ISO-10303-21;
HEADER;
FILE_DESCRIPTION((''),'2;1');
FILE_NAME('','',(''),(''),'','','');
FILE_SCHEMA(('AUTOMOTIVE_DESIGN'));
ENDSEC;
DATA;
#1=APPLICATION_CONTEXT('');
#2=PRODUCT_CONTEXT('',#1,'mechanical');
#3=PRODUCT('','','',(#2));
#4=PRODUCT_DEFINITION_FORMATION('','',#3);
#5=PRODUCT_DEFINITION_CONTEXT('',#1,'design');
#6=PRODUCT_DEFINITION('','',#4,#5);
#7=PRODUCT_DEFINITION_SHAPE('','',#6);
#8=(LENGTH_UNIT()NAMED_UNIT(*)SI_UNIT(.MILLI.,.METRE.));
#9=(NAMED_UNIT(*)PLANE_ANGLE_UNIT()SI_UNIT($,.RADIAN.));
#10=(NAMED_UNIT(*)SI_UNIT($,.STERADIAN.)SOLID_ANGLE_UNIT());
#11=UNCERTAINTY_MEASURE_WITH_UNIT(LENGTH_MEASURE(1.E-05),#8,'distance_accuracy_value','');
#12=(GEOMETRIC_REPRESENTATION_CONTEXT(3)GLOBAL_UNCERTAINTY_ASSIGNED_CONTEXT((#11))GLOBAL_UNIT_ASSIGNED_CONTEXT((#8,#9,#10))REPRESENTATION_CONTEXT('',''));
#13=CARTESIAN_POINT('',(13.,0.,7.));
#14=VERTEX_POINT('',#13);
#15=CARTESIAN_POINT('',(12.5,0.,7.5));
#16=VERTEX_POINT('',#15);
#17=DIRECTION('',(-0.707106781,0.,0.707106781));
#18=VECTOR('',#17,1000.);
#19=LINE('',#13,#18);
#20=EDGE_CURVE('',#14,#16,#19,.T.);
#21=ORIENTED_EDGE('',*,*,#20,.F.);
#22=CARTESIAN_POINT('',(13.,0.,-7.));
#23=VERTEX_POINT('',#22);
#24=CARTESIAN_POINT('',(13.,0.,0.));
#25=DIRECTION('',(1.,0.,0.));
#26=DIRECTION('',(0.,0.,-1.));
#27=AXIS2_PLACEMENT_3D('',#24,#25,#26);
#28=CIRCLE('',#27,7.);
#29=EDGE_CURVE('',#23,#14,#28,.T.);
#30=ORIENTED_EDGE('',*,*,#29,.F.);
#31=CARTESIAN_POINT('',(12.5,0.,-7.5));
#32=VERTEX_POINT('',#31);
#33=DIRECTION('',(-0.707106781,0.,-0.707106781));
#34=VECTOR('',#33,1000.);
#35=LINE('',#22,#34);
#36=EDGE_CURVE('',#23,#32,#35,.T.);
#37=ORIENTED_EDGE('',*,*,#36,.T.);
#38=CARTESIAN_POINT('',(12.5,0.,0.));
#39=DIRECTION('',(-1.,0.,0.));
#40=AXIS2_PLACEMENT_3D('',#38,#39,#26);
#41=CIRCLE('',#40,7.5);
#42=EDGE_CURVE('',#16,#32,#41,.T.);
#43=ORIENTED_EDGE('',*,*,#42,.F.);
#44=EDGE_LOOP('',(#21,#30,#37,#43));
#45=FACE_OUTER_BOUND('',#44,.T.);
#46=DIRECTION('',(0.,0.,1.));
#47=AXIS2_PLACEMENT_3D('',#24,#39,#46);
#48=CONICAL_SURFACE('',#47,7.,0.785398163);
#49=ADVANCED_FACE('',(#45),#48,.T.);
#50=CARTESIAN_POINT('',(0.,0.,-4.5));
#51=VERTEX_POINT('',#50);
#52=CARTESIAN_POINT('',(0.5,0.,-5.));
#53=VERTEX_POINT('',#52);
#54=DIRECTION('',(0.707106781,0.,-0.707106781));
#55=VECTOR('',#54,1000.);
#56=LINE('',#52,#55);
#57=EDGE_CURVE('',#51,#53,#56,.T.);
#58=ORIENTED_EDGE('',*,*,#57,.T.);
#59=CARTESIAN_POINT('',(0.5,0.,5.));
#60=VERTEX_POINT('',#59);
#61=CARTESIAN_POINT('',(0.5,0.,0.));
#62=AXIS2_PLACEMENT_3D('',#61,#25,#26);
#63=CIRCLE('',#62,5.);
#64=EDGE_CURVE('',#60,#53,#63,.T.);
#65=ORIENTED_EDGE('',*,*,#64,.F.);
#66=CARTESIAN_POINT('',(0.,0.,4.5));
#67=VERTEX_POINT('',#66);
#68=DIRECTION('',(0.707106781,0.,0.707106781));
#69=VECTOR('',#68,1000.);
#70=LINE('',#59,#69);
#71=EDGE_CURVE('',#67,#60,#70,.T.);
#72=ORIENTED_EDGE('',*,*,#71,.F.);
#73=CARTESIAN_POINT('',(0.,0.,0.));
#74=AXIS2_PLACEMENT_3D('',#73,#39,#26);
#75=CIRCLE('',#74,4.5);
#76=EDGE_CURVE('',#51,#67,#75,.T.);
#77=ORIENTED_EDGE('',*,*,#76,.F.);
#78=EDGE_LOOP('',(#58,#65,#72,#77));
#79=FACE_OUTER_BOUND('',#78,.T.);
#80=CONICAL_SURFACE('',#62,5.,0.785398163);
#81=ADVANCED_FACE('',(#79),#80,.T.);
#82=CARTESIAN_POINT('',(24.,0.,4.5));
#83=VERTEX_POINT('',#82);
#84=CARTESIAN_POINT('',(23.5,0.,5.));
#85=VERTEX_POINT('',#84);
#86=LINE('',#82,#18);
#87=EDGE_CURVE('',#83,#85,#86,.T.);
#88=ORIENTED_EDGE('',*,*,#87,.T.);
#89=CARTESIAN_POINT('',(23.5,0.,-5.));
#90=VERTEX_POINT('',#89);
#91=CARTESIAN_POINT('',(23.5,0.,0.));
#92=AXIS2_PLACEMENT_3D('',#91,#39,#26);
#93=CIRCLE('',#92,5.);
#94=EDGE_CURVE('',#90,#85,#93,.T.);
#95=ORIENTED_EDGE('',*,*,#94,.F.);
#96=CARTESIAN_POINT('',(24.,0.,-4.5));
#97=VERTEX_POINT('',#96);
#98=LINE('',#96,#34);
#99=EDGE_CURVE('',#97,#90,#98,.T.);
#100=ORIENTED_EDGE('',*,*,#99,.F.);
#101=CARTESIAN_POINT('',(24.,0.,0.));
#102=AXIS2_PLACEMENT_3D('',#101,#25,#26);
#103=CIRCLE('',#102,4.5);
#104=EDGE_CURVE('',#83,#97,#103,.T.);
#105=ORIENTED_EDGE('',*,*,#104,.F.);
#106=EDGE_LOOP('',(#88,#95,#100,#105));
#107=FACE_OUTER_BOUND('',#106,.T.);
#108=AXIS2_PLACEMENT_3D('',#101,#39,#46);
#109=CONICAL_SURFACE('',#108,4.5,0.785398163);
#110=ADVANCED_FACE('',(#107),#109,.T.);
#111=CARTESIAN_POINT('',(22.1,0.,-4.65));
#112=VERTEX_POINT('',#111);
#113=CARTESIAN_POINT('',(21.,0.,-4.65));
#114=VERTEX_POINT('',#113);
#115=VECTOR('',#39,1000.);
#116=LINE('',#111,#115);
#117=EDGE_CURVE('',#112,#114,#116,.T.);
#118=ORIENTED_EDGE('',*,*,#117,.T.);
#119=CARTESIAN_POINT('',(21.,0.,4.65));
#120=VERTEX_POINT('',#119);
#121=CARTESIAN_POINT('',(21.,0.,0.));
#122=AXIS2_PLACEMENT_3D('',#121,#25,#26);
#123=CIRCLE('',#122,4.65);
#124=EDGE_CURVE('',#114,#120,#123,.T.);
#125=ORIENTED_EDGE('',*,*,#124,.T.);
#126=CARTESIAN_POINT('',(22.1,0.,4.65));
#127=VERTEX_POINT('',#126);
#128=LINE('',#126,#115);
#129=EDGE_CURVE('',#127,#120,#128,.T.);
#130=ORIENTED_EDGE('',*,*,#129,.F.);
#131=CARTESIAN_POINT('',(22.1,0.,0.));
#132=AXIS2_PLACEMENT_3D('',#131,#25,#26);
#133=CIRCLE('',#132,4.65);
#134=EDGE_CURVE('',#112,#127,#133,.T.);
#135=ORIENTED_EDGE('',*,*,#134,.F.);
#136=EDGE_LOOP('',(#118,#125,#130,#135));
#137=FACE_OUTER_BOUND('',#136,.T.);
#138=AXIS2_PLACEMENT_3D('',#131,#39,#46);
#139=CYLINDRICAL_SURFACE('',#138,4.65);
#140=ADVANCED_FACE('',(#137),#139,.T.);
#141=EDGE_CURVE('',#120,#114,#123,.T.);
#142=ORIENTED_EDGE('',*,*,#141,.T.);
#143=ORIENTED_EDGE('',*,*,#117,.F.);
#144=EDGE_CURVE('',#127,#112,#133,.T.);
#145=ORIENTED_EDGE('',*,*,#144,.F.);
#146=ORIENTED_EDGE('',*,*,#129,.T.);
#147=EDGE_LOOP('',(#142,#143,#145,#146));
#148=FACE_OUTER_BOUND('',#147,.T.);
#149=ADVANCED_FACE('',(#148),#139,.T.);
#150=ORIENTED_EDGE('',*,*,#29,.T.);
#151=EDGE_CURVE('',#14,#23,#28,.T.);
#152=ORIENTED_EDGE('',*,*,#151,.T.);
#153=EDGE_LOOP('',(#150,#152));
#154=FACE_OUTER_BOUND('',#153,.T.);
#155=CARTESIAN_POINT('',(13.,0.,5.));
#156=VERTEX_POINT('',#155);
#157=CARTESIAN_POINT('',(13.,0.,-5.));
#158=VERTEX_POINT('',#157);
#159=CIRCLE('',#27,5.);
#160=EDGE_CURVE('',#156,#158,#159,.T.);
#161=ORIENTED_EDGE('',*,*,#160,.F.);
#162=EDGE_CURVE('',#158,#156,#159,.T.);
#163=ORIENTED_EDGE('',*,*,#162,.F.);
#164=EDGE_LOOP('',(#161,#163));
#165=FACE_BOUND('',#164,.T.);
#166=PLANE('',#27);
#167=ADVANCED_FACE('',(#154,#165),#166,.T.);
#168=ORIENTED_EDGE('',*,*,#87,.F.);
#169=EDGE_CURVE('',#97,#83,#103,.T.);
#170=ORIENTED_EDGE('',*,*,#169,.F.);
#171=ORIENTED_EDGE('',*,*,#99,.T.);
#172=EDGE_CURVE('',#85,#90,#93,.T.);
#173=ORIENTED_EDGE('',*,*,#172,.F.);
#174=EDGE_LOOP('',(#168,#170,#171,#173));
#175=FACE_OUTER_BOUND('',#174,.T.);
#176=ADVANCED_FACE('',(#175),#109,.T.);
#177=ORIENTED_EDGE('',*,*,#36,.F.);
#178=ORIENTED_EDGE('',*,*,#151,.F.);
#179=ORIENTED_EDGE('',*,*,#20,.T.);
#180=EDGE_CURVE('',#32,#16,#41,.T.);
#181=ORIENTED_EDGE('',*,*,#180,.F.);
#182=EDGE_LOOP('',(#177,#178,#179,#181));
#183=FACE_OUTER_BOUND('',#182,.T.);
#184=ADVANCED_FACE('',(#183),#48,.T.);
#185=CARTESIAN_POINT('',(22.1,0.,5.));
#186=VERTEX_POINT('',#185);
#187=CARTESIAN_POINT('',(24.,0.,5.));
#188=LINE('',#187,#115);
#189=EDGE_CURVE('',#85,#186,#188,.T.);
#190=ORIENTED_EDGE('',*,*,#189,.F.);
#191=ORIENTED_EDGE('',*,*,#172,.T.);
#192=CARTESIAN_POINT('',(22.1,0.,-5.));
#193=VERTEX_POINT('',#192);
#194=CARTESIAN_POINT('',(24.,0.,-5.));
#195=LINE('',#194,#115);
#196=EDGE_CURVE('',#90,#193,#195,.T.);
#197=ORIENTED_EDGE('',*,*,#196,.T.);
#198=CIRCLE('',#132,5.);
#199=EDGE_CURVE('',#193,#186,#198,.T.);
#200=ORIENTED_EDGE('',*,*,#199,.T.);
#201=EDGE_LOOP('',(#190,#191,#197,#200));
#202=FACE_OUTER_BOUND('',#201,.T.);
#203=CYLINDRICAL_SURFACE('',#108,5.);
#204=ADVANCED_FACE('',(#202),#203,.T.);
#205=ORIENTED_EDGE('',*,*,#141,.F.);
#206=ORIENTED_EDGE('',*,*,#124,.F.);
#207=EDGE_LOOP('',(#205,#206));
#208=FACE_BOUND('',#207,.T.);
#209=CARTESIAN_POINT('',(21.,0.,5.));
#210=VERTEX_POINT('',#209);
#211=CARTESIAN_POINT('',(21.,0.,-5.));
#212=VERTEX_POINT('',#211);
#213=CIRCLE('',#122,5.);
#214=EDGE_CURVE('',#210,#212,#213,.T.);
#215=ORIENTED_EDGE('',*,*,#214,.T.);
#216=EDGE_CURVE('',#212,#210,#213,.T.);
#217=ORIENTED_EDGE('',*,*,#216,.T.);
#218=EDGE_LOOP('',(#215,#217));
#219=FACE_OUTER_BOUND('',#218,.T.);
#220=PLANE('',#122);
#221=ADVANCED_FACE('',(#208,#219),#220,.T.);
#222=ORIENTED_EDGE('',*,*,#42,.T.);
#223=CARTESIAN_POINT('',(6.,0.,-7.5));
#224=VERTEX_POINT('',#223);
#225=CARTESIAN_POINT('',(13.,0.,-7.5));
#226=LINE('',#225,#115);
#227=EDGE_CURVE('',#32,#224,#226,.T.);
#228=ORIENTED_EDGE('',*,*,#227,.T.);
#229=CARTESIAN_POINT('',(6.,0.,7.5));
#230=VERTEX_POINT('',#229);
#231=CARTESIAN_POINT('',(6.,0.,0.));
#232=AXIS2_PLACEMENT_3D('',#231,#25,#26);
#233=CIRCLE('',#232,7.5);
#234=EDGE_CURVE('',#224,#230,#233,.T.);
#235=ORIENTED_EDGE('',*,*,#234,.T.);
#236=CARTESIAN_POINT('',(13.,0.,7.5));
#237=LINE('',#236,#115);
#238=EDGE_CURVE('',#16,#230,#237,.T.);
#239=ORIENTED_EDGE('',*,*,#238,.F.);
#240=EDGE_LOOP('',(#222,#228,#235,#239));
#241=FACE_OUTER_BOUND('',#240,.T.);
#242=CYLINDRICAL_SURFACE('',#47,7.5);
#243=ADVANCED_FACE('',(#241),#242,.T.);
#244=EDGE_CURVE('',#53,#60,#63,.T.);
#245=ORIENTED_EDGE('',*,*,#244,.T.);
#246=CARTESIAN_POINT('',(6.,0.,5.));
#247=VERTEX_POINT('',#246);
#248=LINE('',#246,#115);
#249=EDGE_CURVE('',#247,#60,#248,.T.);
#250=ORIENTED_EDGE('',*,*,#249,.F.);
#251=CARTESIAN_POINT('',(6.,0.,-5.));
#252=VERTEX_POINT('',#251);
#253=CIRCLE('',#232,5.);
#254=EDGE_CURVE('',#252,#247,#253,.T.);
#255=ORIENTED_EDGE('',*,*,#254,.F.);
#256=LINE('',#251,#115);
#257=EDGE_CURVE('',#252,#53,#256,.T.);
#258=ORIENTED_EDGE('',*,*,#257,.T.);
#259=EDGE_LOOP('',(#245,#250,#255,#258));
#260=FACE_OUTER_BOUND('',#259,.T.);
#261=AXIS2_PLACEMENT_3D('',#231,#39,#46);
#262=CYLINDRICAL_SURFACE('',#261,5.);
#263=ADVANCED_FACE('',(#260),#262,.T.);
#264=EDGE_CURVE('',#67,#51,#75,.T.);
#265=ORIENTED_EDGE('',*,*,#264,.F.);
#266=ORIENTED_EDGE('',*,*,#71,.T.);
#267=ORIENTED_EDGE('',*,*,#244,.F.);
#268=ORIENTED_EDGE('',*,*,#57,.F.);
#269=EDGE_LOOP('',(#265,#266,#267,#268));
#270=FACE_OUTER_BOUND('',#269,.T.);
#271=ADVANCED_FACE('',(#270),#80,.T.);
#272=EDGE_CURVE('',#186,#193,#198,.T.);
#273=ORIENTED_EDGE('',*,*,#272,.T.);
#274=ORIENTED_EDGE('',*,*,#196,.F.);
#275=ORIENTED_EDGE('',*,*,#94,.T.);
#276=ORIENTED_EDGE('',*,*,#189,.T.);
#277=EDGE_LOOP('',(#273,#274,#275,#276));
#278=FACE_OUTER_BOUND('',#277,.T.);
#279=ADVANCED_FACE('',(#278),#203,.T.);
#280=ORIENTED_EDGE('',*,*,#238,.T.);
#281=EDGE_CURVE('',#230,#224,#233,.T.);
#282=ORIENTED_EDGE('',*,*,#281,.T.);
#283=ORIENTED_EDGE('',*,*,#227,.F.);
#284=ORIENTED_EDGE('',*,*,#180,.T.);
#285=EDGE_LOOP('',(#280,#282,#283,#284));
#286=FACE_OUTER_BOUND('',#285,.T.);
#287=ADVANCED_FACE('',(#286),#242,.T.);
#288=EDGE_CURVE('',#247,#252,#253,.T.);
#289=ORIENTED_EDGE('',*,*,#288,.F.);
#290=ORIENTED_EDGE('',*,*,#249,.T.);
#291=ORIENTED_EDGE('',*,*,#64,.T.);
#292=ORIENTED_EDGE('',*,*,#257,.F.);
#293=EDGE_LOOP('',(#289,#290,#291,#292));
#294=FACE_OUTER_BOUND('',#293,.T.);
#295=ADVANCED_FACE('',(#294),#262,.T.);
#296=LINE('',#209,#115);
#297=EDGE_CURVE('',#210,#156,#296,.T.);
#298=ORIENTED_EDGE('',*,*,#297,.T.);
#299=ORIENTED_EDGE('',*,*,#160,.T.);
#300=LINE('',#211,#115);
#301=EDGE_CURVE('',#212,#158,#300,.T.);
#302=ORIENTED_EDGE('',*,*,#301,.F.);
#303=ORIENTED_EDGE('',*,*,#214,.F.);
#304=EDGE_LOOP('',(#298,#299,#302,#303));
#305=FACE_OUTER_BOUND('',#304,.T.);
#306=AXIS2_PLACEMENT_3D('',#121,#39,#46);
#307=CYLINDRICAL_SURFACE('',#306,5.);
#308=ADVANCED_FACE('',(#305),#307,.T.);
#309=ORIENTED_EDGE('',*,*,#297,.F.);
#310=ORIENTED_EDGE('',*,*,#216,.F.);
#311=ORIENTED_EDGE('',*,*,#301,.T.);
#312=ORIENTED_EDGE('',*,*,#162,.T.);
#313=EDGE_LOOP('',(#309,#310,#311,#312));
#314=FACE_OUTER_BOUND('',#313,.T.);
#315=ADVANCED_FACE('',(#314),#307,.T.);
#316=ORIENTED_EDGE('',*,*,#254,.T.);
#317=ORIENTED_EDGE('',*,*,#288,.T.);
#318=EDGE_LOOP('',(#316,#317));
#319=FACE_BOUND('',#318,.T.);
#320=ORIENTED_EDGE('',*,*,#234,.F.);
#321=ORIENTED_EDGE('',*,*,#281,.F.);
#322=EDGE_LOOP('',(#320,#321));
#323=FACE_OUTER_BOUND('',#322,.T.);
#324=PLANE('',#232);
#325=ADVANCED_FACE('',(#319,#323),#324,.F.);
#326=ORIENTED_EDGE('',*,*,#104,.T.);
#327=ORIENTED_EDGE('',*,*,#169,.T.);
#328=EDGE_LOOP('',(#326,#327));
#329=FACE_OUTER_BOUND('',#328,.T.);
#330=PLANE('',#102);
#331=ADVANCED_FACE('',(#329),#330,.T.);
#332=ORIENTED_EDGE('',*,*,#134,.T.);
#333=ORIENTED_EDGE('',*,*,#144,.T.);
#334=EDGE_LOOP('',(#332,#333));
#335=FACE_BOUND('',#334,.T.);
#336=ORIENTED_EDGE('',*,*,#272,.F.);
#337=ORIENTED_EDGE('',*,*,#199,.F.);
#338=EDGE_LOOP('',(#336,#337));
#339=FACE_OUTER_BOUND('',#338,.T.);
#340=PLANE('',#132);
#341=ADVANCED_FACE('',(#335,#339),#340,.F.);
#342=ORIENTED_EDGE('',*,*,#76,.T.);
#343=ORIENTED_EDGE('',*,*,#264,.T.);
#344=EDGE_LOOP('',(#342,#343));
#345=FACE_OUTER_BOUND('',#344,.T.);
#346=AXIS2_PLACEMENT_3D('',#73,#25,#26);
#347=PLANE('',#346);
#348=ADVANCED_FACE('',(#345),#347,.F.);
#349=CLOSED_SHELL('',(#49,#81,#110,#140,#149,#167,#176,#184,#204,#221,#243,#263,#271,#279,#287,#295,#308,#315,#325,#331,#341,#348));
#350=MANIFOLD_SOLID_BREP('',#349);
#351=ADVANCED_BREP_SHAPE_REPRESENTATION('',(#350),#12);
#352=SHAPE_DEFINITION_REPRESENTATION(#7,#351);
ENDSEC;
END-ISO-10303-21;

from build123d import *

# Parameters (mm, degrees)
SKETCH_1_R      = 5
EXTRUDE_1_DEPTH = 6
CHAMFER_1_SIZE  = 0.5
SKETCH_2_R      = 7.5
EXTRUDE_2_DEPTH = 7
CHAMFER_2_SIZE  = 0.5
SKETCH_3_R      = 5
EXTRUDE_3_DEPTH = 8
SKETCH_4_R      = 4.65
EXTRUDE_4_DEPTH = 1.1
SKETCH_5_R      = 5
EXTRUDE_5_DEPTH = 1.9
CHAMFER_3_SIZE  = 0.5


with BuildPart() as part:
    # 草图1 → 凸台-拉伸1 (new body)
    with BuildSketch(Plane(origin=(0, 0, 0), x_dir=(0, 0, -1), z_dir=(1, 0, 0))):
        Circle(SKETCH_1_R)
    extrude(amount=EXTRUDE_1_DEPTH)

    # 倒角1
    chamfer_1_edges = [part.edges().sort_by_distance(p)[0] for p in [
        (0, 0, 5),
    ]]
    chamfer(chamfer_1_edges, length=CHAMFER_1_SIZE)

    # 草图2 → 凸台-拉伸2 (add)
    with BuildSketch(Plane(origin=(6, 0, 0), x_dir=(0, 0, -1), z_dir=(1, 0, 0))):
        Circle(SKETCH_2_R)
    extrude(amount=EXTRUDE_2_DEPTH)

    # 倒角2
    chamfer_2_edges = [part.edges().sort_by_distance(p)[0] for p in [
        (13, 0, 7.5),
    ]]
    chamfer(chamfer_2_edges, length=CHAMFER_2_SIZE)

    # 草图3 → 凸台-拉伸3 (add)
    with BuildSketch(Plane(origin=(13, 0, 0), x_dir=(0, 0, -1), z_dir=(1, 0, 0))):
        Circle(SKETCH_3_R)
    extrude(amount=EXTRUDE_3_DEPTH)

    # 草图4 → 凸台-拉伸4 (add)
    with BuildSketch(Plane(origin=(21, 0, 0), x_dir=(0, 0, -1), z_dir=(1, 0, 0))):
        Circle(SKETCH_4_R)
    extrude(amount=EXTRUDE_4_DEPTH)

    # 草图5 → 凸台-拉伸5 (add)
    with BuildSketch(Plane(origin=(22.1, 0, 0), x_dir=(0, 0, -1), z_dir=(1, 0, 0))):
        Circle(SKETCH_5_R)
    extrude(amount=EXTRUDE_5_DEPTH)

    # 倒角3
    chamfer_3_edges = [part.edges().sort_by_distance(p)[0] for p in [
        (24, 0, 5),
    ]]
    chamfer(chamfer_3_edges, length=CHAMFER_3_SIZE)


solid = part.part
